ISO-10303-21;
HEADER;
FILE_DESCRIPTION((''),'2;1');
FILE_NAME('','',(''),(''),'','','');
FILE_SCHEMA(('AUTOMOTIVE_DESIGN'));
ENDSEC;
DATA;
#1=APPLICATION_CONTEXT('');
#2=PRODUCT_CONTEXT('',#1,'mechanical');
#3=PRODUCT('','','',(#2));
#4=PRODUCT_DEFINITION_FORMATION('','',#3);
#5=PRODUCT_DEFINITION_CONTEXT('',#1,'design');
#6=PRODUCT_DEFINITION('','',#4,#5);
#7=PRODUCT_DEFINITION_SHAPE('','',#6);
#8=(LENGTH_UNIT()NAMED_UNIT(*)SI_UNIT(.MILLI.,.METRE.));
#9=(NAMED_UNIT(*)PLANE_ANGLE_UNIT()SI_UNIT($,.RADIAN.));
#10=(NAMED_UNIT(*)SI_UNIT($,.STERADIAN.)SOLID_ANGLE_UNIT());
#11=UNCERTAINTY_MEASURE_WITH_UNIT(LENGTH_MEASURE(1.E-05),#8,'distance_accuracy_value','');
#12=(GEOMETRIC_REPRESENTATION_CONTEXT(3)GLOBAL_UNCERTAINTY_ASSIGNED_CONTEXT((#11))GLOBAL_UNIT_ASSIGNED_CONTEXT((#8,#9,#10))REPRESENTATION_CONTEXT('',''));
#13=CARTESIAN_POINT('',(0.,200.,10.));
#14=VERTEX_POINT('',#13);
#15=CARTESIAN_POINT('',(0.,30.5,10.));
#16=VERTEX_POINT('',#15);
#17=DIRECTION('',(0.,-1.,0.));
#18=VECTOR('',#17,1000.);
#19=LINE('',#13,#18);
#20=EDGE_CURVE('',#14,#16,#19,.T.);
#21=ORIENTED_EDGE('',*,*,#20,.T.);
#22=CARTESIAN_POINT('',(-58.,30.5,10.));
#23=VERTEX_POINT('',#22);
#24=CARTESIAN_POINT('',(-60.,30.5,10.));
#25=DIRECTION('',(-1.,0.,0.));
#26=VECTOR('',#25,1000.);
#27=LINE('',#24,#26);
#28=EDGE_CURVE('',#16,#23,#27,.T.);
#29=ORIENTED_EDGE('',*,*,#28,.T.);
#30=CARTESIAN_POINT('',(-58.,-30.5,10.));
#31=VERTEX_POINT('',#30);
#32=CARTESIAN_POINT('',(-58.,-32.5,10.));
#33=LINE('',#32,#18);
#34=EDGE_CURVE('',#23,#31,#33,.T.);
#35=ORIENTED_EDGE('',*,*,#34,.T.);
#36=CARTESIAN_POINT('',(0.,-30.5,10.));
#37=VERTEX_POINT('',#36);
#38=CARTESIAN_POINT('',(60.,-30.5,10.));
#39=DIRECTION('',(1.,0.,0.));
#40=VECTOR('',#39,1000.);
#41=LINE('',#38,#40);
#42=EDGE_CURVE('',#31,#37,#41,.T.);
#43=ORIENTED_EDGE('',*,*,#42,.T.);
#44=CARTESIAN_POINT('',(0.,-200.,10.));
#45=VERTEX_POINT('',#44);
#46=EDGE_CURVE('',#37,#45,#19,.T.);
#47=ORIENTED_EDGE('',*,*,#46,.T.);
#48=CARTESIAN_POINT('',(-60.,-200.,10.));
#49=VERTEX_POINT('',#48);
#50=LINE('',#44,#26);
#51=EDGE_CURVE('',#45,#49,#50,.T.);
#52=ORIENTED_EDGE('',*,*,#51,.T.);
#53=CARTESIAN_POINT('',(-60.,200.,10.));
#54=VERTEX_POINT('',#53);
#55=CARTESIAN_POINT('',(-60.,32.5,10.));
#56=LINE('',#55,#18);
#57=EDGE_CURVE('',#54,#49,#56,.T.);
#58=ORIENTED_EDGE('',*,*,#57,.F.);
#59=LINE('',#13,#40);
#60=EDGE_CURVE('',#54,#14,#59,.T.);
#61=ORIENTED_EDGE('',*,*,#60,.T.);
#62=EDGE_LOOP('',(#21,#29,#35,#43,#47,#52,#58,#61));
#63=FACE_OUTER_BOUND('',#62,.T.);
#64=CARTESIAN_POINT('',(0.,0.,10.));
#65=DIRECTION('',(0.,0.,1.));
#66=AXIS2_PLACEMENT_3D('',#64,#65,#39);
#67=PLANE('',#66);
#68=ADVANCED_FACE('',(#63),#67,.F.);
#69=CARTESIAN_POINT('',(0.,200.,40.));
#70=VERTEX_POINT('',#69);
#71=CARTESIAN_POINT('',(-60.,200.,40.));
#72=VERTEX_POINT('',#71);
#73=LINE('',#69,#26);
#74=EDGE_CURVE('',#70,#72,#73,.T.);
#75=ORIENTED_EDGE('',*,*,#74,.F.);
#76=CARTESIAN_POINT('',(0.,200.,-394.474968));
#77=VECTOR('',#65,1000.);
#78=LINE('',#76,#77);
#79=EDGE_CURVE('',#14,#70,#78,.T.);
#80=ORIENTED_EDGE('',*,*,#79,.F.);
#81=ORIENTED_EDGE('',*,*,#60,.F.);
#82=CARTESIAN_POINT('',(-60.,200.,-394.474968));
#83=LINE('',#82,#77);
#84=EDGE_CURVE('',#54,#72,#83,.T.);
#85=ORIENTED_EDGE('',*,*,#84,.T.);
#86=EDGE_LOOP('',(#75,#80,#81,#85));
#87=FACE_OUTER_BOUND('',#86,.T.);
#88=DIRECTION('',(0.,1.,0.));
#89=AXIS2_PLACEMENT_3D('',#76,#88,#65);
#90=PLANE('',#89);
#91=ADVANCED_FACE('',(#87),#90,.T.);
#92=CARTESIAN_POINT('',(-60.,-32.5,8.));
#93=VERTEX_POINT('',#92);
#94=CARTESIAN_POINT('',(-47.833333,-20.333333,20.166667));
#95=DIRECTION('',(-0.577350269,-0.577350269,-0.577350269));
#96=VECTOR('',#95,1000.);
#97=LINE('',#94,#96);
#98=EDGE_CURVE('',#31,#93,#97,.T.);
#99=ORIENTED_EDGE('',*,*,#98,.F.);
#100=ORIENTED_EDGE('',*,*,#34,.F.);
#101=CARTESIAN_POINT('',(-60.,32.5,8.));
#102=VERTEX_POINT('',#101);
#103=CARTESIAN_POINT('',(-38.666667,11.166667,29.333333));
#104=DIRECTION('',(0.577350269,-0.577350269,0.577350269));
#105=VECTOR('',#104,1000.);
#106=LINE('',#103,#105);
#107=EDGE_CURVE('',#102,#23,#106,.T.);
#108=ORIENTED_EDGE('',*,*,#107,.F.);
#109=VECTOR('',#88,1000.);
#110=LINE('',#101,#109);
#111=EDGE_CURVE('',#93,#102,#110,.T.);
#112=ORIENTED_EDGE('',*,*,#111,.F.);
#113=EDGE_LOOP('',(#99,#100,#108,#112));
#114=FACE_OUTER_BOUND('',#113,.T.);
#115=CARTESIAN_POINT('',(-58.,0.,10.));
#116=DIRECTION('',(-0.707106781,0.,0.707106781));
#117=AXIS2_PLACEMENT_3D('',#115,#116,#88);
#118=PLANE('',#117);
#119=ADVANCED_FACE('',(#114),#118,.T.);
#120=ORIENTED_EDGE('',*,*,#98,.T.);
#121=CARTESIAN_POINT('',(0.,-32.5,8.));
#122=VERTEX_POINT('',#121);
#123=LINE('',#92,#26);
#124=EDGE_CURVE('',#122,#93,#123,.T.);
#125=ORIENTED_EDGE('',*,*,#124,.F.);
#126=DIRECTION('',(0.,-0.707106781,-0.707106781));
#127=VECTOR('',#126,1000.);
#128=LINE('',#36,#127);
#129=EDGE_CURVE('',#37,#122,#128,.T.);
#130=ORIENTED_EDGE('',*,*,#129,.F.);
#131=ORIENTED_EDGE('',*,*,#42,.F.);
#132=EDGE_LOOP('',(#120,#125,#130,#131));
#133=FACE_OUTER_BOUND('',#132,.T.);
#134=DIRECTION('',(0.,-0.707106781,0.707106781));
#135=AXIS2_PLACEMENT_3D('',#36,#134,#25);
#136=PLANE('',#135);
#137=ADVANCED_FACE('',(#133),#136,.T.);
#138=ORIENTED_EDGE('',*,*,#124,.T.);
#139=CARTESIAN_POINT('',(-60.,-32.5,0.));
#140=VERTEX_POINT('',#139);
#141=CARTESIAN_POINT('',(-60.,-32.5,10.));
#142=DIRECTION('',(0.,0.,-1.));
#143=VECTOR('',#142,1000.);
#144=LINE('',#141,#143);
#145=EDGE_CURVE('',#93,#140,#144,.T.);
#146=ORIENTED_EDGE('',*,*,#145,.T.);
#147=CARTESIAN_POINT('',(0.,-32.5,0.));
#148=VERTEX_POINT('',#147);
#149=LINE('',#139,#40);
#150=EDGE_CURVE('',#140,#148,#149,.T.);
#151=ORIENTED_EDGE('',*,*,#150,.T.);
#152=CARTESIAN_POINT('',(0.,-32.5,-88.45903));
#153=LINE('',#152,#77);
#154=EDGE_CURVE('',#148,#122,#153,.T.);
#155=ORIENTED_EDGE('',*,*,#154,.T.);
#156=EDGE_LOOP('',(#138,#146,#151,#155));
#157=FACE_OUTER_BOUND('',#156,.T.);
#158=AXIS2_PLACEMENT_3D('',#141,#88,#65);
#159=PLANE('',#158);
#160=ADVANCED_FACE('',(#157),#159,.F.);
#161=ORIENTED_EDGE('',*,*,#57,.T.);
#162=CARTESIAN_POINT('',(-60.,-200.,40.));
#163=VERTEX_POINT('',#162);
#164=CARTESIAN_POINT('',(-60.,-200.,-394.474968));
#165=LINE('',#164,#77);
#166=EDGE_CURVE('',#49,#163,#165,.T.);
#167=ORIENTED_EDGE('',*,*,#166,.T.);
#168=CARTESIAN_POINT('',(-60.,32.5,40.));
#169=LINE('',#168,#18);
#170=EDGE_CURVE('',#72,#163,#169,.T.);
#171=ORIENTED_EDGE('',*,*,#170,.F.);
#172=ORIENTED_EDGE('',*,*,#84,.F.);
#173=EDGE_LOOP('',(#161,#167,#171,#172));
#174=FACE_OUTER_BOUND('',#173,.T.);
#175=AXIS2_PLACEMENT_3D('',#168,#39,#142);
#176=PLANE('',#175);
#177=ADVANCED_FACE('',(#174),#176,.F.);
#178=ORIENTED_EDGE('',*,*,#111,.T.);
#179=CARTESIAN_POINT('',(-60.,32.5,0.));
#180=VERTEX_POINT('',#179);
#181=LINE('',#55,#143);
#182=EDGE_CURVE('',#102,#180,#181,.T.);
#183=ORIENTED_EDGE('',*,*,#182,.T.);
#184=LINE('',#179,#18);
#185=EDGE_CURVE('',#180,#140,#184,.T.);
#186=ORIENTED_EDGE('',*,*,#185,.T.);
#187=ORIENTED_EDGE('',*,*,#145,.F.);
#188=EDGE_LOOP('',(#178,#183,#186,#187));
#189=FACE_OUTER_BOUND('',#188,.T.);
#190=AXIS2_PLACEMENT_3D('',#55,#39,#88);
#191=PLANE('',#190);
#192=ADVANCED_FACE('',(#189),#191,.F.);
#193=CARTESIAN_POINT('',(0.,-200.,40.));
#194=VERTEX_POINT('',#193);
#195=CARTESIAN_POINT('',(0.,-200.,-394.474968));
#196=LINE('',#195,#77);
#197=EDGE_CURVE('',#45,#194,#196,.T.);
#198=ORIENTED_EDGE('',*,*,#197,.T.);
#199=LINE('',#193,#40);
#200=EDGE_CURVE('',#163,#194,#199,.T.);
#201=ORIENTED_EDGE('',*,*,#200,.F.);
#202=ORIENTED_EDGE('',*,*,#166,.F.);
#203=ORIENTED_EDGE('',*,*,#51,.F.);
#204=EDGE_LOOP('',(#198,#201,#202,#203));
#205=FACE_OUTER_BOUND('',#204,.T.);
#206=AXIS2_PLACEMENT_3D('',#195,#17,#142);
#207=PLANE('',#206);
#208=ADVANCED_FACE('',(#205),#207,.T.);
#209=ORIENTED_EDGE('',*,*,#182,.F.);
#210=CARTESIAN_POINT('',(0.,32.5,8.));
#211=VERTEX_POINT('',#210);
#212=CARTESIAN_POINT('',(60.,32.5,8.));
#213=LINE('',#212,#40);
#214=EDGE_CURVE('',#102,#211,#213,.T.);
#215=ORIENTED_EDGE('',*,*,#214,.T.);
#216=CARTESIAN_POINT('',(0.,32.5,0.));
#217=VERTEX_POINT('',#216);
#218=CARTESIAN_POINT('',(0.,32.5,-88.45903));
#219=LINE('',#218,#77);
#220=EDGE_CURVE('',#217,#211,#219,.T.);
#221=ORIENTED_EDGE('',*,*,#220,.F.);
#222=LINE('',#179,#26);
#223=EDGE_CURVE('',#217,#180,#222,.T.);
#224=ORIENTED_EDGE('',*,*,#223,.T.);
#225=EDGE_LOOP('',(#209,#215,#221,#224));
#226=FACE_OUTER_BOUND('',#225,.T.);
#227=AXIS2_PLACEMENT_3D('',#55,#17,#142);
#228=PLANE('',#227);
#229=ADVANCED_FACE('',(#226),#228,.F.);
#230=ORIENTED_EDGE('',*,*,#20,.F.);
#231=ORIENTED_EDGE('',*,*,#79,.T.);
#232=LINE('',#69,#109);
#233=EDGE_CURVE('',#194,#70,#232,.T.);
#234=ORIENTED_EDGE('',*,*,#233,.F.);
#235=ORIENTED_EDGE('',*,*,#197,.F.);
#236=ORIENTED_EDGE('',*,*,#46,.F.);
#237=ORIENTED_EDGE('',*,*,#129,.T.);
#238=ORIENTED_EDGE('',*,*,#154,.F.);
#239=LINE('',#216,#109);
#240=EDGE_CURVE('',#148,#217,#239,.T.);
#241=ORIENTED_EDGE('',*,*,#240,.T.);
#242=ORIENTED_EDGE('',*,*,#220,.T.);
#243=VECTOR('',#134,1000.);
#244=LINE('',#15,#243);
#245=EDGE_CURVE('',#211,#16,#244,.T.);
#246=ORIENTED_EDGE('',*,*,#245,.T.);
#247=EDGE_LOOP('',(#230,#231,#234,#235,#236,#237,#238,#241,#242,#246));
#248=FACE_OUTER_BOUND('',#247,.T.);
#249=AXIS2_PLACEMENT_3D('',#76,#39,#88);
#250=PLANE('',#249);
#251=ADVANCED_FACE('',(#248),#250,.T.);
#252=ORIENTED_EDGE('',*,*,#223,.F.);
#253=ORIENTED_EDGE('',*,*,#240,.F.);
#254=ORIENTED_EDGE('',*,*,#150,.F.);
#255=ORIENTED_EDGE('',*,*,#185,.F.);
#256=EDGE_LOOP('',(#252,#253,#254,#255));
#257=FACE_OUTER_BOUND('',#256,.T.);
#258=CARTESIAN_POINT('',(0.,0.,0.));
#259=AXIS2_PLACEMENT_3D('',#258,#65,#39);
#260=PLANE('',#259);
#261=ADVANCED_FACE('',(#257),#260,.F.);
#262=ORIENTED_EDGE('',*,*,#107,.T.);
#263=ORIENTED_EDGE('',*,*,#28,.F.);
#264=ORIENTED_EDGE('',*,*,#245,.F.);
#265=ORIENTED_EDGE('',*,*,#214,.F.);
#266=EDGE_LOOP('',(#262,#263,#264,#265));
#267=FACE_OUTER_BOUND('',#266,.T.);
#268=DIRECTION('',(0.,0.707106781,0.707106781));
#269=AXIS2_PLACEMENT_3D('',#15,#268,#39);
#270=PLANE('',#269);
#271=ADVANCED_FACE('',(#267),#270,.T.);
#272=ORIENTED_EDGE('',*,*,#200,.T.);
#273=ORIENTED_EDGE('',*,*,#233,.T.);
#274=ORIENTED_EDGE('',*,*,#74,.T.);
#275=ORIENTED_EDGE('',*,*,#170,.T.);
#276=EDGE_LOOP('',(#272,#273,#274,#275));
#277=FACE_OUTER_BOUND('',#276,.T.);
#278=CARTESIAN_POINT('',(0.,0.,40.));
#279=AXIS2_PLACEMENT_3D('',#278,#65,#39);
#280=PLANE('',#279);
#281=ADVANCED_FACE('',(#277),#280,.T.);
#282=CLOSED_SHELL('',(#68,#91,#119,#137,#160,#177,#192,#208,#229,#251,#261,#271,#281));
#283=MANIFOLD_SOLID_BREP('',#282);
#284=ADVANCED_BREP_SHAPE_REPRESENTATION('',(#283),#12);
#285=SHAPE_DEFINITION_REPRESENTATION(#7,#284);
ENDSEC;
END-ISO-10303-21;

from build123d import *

# Parameters (mm, degrees)
SKETCH_1_W                   = 120
SKETCH_1_H                   = 65
EXTRUDE_1_DEPTH              = 10
CHAMFER_1_SIZE               = 2
SKETCH_2_W                   = 120
SKETCH_2_H                   = 65
EXTRUDE_2_DEPTH              = 30
SKETCH_3_R                   = 10
CUT_EXTRUDE_1_DEPTH          = 2
HOLE_WIZARD_M6_1_D           = 6.6
HOLE_WIZARD_M6_1_CBORE_D     = 13
HOLE_WIZARD_M6_1_CBORE_DEPTH = 35
SKETCH_6_W                   = 60
SKETCH_6_H                   = 400
EXTRUDE_3_DEPTH              = 30
SKETCH_7_W                   = 60
SKETCH_7_H                   = 65
CUT_EXTRUDE_2_DEPTH          = 40


with BuildPart() as part:
    # 草图1 → 凸台-拉伸1 (new body)
    with BuildSketch(Plane.XY):
        Rectangle(SKETCH_1_W, SKETCH_1_H)
    extrude(amount=EXTRUDE_1_DEPTH)

    # 倒角1
    chamfer_1_edges = [part.edges().sort_by_distance(p)[0] for p in [
        (-60, 0, 10),
        (0, -32.5, 10),
        (60, 0, 10),
        (0, 32.5, 10),
    ]]
    chamfer(chamfer_1_edges, length=CHAMFER_1_SIZE)

    # 草图2 → 凸台-拉伸2 (add)
    with BuildSketch(Plane.XY.offset(10)):
        Rectangle(SKETCH_2_W, SKETCH_2_H)
    extrude(amount=EXTRUDE_2_DEPTH)

    # 草图3 → 切除-拉伸1 (cut)
    with BuildSketch(Plane(origin=(0, 0, 0), x_dir=(-1, 0, 0), z_dir=(0, 0, -1))):
        with Locations((-32.5, 0)):
            Circle(SKETCH_3_R)
    extrude(amount=-CUT_EXTRUDE_1_DEPTH, mode=Mode.SUBTRACT)

    # M6 六角头螺栓的柱形沉头孔1 (through all)
    with Locations(Plane.XY.offset(40)):
        with Locations((32.5, 0)):
            CounterBoreHole(HOLE_WIZARD_M6_1_D / 2, HOLE_WIZARD_M6_1_CBORE_D / 2, HOLE_WIZARD_M6_1_CBORE_DEPTH)

    # 草图6 → 凸台-拉伸3 (add)
    with BuildSketch(Plane.XY.offset(40)):
        with Locations((-30, 0)):
            Rectangle(SKETCH_6_W, SKETCH_6_H)
    extrude(amount=-EXTRUDE_3_DEPTH)

    # 草图7 → 切除-拉伸2 (cut)
    with BuildSketch(Plane.XY.offset(40)):
        with Locations((30, 0)):
            Rectangle(SKETCH_7_W, SKETCH_7_H)
    extrude(amount=-CUT_EXTRUDE_2_DEPTH, mode=Mode.SUBTRACT)


solid = part.part
